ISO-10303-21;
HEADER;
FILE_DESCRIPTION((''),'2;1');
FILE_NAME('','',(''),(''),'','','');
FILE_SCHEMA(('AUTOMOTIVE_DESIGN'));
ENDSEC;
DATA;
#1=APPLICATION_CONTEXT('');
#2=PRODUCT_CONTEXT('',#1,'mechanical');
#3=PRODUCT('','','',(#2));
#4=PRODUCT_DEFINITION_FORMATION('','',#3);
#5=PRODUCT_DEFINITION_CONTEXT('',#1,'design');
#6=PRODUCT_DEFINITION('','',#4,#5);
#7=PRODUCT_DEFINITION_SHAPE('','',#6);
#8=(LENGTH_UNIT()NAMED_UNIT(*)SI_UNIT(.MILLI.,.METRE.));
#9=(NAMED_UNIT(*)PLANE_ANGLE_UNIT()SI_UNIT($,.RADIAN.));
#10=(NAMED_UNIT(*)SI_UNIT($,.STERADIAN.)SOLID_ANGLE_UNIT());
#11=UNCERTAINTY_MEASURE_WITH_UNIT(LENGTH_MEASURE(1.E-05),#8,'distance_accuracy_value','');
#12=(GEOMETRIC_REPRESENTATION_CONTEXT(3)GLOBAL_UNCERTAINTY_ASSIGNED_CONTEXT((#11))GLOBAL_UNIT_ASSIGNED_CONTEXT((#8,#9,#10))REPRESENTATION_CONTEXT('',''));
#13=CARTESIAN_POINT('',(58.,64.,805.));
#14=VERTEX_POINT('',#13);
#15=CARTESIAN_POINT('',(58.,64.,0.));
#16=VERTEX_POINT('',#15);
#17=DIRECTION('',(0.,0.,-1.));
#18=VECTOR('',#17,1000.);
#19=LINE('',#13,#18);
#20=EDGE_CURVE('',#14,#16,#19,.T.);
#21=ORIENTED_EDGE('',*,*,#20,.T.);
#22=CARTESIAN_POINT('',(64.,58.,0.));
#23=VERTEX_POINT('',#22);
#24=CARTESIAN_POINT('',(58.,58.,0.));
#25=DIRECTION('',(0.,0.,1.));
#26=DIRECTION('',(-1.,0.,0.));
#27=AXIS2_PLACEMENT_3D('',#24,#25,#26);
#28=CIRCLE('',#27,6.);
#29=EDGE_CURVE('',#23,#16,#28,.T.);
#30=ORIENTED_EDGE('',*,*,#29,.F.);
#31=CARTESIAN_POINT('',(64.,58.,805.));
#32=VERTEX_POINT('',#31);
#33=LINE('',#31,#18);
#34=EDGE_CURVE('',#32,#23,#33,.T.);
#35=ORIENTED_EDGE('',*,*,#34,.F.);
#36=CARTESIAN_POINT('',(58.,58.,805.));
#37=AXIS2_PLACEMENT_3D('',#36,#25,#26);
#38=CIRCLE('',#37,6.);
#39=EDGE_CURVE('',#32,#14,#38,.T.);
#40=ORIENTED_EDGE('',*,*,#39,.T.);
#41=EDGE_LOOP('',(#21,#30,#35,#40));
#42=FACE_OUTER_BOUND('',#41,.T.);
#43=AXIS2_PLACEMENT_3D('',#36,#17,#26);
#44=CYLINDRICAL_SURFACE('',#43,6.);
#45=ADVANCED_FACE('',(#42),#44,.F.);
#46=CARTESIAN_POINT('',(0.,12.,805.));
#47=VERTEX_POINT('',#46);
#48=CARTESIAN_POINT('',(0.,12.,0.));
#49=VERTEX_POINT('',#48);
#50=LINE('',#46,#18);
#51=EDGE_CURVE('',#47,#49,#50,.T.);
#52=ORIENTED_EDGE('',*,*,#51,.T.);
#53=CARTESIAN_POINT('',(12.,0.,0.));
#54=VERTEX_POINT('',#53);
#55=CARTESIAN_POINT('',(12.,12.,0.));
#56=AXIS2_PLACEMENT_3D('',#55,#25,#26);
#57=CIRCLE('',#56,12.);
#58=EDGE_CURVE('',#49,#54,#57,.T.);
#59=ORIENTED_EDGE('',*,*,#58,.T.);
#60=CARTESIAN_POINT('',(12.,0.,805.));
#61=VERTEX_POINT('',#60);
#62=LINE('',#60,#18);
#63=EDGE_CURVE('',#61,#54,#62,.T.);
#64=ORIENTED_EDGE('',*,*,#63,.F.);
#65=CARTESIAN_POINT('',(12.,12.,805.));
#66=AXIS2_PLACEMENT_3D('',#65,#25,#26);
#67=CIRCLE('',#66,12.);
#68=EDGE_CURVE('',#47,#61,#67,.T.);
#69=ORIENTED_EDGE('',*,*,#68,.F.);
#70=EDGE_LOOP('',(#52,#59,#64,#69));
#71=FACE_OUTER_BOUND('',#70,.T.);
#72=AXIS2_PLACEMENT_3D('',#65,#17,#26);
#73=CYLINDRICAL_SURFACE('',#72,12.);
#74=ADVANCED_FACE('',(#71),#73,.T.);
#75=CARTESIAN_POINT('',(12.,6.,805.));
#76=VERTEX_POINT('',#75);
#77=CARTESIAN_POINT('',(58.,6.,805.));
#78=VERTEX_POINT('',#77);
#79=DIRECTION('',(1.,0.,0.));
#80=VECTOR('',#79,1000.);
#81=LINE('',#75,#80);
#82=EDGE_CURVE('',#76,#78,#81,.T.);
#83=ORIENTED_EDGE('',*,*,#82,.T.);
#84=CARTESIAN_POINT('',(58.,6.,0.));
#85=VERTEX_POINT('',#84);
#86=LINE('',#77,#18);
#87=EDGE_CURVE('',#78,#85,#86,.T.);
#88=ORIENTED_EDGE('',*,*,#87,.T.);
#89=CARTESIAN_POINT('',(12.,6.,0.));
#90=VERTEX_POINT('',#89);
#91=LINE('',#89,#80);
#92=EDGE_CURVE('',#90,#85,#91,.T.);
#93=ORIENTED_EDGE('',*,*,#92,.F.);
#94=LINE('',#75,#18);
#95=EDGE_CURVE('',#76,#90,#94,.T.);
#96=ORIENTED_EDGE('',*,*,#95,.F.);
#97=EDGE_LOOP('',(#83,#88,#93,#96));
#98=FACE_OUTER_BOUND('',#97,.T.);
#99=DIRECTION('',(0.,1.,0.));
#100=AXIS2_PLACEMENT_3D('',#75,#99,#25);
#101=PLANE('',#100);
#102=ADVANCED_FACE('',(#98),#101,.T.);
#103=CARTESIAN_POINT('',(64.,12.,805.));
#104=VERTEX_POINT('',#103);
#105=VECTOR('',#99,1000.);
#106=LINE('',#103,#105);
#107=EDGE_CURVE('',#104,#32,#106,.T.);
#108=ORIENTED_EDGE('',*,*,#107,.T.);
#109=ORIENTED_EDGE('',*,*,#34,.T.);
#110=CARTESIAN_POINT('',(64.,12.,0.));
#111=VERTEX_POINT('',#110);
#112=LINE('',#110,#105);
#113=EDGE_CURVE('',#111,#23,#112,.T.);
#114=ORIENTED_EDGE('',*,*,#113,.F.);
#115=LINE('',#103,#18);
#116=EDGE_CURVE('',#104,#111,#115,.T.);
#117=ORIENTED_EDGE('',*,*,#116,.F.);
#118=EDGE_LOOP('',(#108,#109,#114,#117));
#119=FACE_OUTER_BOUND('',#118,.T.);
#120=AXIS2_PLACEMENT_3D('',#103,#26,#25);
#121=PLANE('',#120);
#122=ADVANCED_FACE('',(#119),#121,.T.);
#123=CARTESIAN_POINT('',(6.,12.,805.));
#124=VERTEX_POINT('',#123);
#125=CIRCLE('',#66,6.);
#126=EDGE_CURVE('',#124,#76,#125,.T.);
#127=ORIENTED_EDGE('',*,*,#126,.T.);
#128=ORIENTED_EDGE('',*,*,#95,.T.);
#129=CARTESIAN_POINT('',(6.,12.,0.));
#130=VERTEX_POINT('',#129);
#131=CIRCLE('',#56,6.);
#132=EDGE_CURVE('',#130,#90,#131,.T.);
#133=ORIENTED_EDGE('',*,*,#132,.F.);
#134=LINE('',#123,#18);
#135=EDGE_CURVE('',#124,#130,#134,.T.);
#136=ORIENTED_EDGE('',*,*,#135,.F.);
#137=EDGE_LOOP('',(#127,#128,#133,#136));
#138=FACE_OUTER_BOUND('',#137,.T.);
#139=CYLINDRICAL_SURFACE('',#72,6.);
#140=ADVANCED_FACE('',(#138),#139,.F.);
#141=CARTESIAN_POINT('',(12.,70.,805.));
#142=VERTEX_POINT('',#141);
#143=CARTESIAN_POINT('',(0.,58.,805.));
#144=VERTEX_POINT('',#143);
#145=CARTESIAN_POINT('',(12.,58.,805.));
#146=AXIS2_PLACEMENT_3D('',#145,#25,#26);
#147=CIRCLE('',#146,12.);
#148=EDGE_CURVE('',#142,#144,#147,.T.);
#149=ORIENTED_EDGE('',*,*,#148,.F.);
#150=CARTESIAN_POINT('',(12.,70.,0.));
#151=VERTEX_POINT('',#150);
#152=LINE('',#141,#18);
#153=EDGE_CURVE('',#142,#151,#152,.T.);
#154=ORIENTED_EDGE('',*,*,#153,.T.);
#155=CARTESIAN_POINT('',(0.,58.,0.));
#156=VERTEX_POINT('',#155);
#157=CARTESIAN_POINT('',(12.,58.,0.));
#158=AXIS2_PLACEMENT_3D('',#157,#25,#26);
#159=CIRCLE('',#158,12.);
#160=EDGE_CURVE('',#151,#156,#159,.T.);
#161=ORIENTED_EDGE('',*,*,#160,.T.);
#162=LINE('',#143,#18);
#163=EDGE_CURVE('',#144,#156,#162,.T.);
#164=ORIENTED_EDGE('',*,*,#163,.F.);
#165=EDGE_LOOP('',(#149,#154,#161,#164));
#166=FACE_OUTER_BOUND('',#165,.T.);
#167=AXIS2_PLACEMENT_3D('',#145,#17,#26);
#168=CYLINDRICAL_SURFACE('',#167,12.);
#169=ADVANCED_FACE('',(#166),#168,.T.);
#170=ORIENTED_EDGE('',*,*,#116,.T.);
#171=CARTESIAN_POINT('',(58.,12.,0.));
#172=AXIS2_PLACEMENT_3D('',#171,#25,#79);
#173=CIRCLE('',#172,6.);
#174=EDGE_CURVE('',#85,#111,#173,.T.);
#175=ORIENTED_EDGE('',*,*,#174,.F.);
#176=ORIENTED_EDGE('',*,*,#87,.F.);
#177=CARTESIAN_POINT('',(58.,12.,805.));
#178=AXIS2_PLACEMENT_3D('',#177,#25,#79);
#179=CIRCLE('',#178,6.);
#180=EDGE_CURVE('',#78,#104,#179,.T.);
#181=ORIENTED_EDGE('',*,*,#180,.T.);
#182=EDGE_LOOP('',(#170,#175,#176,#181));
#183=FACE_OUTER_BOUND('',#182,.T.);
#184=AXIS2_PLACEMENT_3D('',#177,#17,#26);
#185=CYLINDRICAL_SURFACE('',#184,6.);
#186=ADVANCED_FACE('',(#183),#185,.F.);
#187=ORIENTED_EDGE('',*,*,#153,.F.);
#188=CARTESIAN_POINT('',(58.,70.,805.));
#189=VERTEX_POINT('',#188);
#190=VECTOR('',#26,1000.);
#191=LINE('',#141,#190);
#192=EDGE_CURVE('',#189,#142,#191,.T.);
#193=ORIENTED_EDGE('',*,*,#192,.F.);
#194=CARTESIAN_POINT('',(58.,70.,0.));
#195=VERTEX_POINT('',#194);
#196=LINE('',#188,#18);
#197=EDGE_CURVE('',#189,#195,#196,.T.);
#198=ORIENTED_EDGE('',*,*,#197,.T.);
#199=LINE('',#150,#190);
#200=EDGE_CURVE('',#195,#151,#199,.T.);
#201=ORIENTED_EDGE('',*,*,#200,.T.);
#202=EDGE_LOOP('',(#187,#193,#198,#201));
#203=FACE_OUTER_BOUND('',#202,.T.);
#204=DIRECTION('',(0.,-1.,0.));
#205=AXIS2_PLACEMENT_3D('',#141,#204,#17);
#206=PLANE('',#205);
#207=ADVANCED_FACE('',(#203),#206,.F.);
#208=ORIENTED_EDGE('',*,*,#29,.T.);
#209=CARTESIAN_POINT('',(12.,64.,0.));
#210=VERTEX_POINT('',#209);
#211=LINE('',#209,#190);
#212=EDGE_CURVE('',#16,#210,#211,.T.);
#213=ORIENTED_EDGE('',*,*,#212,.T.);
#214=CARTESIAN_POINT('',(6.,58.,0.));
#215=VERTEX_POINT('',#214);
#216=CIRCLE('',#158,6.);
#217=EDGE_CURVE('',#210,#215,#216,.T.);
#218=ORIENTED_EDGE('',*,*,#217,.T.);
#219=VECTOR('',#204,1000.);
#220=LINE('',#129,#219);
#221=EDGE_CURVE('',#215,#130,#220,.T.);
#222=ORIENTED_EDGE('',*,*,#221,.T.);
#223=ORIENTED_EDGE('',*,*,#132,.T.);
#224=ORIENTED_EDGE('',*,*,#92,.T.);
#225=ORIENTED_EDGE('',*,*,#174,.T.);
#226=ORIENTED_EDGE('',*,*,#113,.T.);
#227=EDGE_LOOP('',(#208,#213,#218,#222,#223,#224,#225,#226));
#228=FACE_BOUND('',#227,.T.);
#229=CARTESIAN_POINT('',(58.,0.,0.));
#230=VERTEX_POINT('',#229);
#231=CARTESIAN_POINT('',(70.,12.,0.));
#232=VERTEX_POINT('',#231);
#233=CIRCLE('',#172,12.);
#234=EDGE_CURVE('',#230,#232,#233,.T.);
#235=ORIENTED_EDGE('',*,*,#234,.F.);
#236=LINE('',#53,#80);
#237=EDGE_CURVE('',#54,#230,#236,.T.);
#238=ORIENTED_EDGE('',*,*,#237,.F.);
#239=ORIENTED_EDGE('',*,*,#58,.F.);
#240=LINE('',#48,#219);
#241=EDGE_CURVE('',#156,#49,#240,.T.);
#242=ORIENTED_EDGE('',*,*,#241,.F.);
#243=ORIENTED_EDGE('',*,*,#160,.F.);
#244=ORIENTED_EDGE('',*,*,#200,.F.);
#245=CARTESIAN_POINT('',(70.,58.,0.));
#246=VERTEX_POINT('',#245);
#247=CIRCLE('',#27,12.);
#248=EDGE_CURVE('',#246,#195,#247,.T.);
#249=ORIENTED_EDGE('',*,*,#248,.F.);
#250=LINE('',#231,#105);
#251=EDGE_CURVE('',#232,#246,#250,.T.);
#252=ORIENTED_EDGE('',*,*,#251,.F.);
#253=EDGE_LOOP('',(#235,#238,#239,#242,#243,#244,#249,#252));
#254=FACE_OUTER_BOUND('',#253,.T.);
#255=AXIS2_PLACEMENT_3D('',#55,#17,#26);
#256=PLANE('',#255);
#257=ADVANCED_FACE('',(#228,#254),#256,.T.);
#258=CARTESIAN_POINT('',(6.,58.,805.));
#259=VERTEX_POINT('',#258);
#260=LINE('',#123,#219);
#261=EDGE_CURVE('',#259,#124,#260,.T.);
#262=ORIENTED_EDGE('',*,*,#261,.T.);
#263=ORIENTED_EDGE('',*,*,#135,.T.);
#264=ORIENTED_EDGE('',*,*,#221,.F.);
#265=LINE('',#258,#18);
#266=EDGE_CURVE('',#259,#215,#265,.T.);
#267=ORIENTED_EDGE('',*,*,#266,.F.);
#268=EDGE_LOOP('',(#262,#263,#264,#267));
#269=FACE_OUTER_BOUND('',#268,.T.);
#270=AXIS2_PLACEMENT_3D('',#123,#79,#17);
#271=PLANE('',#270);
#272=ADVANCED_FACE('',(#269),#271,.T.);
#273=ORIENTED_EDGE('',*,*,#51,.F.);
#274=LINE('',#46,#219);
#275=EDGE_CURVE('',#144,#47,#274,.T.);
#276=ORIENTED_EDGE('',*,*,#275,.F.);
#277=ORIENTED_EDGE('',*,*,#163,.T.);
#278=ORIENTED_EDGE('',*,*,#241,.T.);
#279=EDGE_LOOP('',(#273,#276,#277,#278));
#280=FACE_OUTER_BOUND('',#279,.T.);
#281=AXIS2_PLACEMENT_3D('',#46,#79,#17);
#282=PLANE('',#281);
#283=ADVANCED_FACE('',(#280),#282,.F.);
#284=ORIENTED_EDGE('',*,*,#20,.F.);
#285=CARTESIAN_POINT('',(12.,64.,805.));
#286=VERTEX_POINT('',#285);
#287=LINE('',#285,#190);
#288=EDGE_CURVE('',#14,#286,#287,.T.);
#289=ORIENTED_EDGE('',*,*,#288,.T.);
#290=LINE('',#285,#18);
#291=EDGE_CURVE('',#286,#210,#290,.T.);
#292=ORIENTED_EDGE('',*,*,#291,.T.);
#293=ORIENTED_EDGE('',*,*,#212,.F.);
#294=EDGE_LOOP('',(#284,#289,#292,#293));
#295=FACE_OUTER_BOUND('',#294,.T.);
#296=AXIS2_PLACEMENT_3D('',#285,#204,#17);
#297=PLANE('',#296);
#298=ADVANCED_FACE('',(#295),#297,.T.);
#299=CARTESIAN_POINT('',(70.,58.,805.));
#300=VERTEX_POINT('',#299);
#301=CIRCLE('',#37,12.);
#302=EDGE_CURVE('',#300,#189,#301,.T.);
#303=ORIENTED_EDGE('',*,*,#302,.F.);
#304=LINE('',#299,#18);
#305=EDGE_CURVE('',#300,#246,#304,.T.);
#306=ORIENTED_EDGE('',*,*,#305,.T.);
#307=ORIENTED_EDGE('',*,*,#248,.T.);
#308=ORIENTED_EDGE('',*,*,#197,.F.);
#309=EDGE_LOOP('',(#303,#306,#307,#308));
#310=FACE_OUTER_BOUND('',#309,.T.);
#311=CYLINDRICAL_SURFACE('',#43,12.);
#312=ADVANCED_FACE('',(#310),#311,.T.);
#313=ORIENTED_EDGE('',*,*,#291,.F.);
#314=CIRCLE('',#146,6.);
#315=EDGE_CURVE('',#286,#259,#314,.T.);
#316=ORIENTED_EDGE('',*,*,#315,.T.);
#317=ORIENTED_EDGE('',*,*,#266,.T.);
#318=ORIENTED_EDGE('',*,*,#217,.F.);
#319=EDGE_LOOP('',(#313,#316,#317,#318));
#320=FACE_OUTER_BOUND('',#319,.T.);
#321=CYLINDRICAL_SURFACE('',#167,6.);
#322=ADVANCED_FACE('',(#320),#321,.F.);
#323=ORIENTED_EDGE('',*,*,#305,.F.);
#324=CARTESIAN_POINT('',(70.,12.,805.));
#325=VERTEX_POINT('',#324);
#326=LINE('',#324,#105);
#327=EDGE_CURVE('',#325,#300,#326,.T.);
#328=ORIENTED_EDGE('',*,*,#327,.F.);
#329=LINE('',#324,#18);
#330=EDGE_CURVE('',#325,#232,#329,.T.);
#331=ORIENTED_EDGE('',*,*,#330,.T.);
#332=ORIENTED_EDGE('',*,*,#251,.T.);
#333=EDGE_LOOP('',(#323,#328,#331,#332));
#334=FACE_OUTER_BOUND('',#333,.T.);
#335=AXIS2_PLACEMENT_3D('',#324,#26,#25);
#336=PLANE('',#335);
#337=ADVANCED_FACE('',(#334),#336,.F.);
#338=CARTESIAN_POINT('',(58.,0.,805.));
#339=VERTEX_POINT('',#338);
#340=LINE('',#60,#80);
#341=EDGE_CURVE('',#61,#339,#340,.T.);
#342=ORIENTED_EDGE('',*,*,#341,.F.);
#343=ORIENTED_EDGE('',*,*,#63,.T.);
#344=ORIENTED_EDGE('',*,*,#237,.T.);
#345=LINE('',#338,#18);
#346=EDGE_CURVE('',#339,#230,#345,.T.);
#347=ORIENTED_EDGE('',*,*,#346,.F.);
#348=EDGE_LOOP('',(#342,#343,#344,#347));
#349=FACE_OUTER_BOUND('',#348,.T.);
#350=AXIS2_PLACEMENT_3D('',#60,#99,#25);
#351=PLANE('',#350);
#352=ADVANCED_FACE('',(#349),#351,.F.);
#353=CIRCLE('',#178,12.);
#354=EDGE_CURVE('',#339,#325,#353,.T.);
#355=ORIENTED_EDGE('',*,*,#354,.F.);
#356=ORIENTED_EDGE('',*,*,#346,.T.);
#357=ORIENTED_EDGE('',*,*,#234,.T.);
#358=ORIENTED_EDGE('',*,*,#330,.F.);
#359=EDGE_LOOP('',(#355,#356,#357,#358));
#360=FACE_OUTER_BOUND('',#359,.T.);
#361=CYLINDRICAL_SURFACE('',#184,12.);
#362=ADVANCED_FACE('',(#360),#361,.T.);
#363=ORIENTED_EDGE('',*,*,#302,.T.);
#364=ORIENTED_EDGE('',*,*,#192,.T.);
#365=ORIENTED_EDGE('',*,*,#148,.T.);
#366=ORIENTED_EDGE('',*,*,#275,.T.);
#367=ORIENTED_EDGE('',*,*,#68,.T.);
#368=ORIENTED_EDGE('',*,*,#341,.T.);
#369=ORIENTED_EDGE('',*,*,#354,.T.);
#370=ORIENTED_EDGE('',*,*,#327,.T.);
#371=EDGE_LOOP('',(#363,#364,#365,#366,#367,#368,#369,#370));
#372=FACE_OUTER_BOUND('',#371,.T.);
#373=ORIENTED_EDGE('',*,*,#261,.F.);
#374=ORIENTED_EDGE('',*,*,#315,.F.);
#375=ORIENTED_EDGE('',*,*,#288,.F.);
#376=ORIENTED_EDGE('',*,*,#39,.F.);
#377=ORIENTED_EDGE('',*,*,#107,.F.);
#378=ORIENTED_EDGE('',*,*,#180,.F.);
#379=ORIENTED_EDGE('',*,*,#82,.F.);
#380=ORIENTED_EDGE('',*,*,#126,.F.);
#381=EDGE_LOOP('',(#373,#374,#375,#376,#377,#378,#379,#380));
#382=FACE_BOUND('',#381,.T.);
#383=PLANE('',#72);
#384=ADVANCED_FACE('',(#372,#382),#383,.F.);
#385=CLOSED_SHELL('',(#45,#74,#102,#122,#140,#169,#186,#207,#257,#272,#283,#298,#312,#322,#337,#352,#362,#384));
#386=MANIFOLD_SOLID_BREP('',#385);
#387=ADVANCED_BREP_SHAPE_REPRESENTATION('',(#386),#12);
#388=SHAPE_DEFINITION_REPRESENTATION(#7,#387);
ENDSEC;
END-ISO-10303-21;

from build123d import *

# Parameters (mm, degrees)
BOSS_EXTRUDE1_DEPTH = 805


with BuildPart() as part:
    # Sketch1 → Boss-Extrude1 (new body)
    with BuildSketch(Plane.XY):
        with BuildLine():
            Line((12, 0), (58, 0))
            ThreePointArc((58, 0), (66.485281374, 3.514718626), (70, 12))
            Line((70, 12), (70, 58))
            ThreePointArc((70, 58), (66.485281374, 66.485281374), (58, 70))
            Line((58, 70), (12, 70))
            ThreePointArc((12, 70), (3.514718626, 66.485281374), (0, 58))
            Line((0, 58), (0, 12))
            ThreePointArc((0, 12), (3.514718626, 3.514718626), (12, 0))
        make_face()
        with BuildLine():
            Line((12, 6), (58, 6))
            ThreePointArc((58, 6), (62.242640687, 7.757359313), (64, 12))
            Line((64, 12), (64, 58))
            ThreePointArc((64, 58), (62.242640687, 62.242640687), (58, 64))
            Line((58, 64), (12, 64))
            ThreePointArc((12, 64), (7.757359313, 62.242640687), (6, 58))
            Line((6, 58), (6, 12))
            ThreePointArc((6, 12), (7.757359313, 7.757359313), (12, 6))
        make_face(mode=Mode.SUBTRACT)
    extrude(amount=BOSS_EXTRUDE1_DEPTH)


solid = part.part
